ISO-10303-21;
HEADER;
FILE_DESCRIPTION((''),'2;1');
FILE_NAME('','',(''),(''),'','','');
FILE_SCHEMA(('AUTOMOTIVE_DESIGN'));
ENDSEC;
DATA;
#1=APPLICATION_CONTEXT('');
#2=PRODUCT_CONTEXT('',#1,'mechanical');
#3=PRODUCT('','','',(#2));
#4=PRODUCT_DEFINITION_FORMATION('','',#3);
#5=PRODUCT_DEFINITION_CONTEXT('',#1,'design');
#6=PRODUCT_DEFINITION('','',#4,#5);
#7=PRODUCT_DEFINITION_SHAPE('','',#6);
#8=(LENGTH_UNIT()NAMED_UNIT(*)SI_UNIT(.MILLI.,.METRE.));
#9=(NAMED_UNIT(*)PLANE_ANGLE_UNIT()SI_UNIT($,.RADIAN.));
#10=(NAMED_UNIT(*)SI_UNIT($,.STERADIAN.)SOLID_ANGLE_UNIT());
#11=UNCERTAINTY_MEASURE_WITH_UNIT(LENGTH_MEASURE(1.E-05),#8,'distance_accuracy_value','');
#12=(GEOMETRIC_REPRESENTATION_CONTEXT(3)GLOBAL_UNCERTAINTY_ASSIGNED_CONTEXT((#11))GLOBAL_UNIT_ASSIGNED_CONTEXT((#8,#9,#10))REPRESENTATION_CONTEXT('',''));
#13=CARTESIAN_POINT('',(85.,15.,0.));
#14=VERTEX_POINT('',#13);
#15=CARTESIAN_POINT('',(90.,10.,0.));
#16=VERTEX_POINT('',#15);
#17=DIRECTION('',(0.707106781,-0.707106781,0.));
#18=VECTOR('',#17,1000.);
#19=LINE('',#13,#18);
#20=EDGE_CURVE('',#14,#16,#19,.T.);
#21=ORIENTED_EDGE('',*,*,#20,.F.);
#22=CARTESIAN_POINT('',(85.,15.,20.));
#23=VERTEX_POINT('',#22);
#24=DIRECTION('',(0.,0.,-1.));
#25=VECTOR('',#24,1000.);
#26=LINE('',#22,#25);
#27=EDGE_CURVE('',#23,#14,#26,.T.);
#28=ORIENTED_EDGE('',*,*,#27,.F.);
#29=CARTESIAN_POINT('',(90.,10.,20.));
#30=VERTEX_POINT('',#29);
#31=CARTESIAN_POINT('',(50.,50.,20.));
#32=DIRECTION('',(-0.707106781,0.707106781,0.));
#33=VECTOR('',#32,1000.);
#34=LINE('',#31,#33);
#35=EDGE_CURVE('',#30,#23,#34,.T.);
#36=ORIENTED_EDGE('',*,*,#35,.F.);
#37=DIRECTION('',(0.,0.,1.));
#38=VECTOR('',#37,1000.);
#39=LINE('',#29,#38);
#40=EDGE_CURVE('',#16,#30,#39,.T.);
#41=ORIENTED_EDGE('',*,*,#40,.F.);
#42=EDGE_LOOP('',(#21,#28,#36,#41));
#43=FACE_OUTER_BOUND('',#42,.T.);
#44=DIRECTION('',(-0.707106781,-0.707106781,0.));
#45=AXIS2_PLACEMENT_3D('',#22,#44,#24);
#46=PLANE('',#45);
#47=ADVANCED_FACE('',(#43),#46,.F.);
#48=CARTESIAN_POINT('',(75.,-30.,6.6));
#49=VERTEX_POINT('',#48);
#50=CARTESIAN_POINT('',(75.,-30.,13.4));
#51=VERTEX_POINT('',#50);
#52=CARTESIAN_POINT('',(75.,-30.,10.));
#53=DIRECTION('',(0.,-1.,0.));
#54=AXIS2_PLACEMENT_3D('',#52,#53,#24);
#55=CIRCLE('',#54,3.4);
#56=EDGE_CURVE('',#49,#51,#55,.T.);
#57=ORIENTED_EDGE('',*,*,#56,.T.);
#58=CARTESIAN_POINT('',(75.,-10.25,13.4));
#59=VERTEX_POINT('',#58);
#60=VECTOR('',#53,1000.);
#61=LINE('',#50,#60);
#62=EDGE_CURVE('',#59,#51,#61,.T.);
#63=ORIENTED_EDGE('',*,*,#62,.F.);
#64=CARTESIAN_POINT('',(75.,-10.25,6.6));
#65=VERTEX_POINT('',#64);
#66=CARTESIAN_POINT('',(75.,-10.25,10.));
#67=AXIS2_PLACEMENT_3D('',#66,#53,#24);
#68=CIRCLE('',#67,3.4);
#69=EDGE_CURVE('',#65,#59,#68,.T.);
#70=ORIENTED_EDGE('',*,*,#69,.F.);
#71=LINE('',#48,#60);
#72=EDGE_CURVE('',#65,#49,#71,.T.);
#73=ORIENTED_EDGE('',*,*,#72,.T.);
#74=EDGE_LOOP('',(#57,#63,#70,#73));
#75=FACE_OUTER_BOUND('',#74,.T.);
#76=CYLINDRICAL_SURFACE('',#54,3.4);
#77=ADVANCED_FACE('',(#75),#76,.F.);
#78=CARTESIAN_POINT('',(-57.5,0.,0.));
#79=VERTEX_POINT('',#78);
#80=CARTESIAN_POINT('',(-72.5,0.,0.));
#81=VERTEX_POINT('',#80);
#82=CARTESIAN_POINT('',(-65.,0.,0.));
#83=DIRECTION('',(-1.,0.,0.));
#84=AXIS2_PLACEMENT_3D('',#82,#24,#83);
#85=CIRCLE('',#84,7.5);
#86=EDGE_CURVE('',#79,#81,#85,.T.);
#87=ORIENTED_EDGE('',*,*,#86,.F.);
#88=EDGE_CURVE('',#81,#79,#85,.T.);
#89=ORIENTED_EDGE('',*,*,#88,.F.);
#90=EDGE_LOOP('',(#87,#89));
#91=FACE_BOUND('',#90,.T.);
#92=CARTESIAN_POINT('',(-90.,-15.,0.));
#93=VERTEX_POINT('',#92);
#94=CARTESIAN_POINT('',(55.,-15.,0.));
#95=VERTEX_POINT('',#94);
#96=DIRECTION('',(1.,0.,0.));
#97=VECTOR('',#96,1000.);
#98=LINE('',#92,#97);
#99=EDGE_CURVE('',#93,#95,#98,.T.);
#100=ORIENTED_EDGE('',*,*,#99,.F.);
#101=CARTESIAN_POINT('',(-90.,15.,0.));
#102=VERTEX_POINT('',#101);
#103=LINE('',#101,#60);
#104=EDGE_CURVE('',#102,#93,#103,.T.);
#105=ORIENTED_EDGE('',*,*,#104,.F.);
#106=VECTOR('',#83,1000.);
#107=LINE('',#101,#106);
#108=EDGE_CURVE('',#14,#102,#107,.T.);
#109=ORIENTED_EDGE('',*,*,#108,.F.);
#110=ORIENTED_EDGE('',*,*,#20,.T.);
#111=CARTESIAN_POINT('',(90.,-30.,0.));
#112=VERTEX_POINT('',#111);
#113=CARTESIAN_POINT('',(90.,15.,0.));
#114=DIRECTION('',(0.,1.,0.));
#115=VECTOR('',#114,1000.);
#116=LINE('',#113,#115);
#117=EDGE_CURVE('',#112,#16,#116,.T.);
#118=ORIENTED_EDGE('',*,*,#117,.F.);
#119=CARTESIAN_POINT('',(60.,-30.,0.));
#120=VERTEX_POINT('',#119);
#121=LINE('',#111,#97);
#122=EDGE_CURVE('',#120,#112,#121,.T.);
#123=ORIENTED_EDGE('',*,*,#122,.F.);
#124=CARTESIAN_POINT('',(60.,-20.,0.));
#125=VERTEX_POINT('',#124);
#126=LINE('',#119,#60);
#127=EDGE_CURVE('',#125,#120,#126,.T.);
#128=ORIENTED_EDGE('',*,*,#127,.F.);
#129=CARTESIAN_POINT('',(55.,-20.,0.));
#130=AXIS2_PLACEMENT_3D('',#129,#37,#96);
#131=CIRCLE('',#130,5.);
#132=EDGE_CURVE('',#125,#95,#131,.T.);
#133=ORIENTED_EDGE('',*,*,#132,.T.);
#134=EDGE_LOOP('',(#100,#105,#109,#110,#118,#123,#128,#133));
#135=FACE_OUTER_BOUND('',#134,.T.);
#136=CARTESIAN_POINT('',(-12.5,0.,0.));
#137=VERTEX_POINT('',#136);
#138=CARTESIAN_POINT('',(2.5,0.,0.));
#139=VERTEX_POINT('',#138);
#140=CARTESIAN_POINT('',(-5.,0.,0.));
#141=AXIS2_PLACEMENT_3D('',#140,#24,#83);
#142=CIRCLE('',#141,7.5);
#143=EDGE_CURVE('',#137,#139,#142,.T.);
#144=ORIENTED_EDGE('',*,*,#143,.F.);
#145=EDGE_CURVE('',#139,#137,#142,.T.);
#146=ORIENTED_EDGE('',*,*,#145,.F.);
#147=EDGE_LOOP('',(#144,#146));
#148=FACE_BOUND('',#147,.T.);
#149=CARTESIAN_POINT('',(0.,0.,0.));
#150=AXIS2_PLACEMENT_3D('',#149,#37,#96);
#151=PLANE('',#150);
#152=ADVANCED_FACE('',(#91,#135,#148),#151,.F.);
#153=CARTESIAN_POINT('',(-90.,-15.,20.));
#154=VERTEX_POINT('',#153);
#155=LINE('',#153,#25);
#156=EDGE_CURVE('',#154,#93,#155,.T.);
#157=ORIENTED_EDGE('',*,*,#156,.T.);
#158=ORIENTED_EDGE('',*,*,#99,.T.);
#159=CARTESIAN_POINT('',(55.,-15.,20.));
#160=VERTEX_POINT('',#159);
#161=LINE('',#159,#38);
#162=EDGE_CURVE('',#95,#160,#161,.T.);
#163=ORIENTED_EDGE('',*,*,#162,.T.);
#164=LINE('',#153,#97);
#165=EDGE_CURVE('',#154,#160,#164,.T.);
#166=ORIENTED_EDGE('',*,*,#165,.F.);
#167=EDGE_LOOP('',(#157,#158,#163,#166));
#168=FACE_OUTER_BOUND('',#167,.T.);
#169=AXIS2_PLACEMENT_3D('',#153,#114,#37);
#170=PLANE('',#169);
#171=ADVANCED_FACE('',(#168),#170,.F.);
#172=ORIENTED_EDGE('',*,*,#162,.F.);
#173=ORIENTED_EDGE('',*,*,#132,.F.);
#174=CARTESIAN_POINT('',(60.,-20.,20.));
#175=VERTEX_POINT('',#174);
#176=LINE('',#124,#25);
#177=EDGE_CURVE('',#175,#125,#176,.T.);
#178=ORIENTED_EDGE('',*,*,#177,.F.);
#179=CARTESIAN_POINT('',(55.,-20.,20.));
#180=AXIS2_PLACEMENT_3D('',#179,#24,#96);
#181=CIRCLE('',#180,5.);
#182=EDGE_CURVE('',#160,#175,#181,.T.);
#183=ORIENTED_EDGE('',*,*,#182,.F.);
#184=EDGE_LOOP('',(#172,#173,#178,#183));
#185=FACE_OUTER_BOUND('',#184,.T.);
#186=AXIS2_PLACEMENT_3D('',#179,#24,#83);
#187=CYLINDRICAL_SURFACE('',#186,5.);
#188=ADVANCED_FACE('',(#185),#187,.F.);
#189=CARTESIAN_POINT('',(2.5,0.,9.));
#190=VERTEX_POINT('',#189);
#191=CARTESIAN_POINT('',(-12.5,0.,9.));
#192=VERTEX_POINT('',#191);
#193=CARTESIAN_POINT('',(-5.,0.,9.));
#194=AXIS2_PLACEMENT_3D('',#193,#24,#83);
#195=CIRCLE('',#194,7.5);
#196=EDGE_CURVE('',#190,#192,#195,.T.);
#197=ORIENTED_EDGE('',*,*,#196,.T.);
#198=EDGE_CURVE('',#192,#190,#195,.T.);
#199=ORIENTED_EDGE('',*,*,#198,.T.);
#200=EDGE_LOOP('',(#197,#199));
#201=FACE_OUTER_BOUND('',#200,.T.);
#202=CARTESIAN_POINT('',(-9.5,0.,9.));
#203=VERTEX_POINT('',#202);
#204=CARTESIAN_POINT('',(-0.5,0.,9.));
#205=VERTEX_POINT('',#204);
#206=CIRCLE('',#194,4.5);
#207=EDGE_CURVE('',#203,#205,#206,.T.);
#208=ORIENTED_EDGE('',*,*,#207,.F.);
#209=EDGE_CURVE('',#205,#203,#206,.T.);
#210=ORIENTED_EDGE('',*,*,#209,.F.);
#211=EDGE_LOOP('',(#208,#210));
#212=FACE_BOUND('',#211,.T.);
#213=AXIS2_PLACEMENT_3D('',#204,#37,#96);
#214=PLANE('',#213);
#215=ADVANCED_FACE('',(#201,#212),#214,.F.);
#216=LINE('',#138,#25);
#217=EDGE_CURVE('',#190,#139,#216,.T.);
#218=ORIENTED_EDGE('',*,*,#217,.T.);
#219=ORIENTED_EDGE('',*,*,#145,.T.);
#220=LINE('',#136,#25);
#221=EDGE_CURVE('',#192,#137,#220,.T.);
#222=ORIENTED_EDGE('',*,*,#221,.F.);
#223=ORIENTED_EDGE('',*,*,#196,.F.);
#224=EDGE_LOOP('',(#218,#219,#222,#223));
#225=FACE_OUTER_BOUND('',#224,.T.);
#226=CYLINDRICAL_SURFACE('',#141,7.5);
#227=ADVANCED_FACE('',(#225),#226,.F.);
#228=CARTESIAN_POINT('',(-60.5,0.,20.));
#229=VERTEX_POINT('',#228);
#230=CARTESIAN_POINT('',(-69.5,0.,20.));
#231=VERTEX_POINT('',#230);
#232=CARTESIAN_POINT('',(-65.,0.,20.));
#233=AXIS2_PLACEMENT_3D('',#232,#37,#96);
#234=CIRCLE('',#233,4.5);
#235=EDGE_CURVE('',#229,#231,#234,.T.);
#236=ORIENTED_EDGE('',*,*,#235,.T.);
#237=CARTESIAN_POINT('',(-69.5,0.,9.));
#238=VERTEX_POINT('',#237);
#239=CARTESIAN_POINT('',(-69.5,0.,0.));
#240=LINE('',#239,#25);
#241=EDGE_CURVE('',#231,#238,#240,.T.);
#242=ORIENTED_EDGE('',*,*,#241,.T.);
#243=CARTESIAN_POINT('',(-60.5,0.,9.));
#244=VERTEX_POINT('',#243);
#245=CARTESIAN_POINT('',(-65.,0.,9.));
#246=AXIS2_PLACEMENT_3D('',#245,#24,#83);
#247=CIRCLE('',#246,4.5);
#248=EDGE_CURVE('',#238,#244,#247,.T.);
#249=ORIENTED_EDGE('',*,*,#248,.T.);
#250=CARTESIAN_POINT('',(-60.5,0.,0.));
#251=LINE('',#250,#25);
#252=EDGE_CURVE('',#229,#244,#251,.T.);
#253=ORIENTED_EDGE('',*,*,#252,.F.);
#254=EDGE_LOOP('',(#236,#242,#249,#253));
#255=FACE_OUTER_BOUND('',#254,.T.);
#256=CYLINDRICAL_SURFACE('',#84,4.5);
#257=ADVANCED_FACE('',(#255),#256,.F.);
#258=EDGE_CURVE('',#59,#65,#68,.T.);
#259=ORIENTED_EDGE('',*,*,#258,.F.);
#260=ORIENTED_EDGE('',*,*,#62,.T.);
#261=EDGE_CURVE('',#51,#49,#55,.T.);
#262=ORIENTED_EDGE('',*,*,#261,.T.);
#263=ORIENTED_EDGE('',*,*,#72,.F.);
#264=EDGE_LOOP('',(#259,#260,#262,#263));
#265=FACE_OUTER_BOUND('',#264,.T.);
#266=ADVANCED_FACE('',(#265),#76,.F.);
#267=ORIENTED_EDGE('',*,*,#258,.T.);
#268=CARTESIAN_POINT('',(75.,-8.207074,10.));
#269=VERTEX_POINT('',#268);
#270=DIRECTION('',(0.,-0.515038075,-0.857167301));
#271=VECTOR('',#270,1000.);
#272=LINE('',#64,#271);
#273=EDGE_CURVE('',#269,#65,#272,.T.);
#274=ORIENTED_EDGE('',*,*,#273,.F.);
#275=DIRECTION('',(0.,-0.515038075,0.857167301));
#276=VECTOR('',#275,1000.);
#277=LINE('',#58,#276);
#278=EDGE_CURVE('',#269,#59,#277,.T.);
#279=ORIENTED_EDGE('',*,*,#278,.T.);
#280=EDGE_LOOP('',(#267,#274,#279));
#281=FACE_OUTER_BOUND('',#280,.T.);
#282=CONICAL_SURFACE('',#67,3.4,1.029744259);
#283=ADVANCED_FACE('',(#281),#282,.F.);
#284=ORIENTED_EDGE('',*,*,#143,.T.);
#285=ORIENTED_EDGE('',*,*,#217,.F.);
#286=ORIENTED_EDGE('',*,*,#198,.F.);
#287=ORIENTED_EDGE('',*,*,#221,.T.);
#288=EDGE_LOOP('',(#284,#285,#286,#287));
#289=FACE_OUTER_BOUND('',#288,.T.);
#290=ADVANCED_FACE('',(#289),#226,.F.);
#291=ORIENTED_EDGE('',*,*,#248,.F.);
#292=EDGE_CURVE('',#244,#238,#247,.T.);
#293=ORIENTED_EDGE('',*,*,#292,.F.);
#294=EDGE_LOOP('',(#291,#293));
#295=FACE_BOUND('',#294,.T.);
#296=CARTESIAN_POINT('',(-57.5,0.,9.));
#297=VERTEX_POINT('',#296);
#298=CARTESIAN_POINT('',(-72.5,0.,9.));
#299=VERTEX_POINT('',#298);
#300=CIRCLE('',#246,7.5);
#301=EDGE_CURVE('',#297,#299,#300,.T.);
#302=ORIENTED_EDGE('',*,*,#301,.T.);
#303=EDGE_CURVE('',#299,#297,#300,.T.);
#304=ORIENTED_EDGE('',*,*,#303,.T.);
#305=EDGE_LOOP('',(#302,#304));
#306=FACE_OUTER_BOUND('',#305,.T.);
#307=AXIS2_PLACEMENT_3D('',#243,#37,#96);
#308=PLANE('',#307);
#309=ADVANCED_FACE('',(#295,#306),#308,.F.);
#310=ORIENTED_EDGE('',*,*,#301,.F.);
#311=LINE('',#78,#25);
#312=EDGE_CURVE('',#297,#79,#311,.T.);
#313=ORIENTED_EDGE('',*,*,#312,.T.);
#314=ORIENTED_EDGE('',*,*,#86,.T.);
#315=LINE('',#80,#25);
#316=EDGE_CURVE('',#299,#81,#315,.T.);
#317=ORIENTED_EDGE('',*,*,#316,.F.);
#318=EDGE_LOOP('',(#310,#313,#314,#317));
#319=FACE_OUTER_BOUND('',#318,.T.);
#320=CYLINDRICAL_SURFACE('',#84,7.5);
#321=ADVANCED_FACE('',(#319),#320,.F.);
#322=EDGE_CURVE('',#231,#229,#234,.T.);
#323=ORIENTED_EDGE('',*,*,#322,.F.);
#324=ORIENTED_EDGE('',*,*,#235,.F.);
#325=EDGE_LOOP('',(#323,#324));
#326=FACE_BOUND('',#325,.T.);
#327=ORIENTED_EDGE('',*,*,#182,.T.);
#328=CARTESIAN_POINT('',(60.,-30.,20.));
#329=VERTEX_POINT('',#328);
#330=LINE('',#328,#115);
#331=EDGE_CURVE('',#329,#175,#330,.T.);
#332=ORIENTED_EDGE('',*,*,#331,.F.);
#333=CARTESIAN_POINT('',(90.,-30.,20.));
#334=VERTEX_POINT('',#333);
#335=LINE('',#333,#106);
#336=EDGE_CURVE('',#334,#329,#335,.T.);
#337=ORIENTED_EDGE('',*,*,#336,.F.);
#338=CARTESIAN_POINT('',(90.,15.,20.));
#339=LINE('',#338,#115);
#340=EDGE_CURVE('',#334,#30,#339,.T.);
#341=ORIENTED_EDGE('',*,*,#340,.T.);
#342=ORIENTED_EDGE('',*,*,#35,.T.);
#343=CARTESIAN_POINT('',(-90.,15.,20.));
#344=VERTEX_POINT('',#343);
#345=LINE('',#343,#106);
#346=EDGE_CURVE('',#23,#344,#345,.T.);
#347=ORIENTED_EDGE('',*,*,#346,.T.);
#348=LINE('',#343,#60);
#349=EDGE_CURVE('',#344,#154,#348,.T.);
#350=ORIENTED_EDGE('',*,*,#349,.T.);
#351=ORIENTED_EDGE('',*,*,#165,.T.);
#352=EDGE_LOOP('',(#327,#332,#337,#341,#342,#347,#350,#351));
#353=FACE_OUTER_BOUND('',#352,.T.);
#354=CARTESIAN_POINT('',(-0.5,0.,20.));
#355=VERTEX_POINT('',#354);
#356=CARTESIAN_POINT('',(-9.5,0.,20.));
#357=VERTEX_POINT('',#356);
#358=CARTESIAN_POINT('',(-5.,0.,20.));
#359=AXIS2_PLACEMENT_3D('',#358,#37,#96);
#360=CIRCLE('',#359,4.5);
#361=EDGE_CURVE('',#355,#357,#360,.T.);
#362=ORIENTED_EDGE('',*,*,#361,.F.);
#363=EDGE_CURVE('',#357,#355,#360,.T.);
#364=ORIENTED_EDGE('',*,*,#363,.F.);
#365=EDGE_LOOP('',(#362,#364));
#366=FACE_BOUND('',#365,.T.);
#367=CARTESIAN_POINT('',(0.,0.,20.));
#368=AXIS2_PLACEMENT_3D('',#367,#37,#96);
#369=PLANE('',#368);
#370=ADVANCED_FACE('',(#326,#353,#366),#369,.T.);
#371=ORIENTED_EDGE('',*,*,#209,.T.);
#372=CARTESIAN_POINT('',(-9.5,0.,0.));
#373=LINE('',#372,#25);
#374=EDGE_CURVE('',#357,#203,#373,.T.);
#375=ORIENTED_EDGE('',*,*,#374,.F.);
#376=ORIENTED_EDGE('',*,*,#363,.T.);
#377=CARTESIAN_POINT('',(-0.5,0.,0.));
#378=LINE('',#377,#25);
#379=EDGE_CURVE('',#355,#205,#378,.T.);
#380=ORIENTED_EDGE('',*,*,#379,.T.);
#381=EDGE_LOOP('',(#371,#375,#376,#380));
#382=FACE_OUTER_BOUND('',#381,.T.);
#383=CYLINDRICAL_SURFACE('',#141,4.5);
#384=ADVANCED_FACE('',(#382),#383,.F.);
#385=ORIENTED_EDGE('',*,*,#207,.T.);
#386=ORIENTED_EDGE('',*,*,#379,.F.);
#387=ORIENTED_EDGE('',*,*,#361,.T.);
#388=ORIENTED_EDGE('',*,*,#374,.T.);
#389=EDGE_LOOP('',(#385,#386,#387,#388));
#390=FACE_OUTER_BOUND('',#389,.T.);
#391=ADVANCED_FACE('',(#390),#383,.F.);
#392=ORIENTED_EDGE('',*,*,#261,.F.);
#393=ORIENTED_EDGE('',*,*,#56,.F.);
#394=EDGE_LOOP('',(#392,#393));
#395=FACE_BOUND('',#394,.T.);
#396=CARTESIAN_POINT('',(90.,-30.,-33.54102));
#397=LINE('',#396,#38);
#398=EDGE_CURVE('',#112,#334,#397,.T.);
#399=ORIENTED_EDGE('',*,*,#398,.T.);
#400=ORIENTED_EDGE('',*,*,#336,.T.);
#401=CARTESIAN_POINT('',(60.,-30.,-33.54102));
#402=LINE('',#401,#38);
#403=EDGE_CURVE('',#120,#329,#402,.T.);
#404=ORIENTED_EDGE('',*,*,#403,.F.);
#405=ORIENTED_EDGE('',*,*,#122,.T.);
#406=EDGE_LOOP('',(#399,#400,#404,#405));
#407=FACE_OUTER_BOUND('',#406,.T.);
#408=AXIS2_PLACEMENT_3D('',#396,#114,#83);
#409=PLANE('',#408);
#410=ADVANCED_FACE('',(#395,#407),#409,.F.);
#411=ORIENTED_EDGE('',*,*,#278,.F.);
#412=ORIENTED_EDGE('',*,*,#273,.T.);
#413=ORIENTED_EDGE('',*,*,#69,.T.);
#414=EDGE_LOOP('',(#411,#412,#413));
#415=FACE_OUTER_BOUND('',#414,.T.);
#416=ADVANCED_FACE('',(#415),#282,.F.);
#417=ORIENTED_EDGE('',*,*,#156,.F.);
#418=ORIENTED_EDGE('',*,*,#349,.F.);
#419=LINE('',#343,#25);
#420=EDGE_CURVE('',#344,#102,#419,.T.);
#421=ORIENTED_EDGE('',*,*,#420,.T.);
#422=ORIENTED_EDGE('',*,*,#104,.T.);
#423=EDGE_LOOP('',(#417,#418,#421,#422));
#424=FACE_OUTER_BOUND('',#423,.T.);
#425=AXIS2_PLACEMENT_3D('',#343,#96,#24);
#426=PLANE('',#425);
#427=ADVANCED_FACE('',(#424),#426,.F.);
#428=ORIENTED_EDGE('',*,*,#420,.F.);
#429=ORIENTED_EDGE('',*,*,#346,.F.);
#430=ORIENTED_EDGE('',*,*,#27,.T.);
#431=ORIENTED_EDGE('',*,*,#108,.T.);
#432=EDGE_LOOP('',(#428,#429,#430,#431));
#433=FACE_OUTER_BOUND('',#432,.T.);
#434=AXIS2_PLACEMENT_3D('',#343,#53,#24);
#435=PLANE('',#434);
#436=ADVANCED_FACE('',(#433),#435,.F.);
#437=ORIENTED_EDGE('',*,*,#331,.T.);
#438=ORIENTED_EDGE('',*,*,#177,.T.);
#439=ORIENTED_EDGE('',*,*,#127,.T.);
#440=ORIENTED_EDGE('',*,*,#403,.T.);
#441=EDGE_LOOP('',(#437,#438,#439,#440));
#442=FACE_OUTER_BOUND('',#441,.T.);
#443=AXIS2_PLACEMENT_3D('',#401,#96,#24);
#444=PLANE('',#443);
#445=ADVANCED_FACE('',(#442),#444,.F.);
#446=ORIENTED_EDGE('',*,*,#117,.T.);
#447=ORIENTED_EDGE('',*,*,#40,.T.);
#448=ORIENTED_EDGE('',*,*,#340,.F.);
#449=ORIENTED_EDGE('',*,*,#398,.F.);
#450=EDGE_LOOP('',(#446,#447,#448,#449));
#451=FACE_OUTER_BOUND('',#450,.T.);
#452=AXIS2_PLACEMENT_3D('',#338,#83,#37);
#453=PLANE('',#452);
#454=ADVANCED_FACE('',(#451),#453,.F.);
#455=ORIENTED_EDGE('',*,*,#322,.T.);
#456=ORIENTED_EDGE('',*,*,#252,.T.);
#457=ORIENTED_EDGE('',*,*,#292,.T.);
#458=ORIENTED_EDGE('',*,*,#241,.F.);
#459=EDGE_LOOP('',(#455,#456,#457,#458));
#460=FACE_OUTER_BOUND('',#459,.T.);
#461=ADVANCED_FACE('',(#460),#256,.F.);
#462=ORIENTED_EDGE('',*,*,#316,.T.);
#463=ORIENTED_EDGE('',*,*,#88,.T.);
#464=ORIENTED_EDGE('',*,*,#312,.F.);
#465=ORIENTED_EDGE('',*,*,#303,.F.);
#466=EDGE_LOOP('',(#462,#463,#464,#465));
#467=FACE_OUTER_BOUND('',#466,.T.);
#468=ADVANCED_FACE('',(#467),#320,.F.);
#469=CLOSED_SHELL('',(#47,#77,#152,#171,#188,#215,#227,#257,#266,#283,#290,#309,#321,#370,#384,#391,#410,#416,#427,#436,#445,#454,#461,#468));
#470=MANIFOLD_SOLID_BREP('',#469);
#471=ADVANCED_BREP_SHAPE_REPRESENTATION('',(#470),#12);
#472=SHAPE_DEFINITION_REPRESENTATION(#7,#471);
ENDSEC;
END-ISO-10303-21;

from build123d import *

# Parameters (mm, degrees)
SKETCH_1_W                = 180
SKETCH_1_H                = 30
EXTRUDE_1_DEPTH           = 20
SKETCH_4_W                = 30
SKETCH_4_H                = 15
EXTRUDE_2_DEPTH           = 20
FILLET_1_R                = 5
CHAMFER_1_SIZE            = 5
HOLE_WIZARD_M8_2_D        = 6.8
HOLE_WIZARD_M8_2_DEPTH    = 19.75
HOLE_WIZARD_M8_2_TIP      = 2.042926105
HOLE_WIZARD_1_D           = 9
HOLE_WIZARD_1_DEPTH       = 27.5
HOLE_WIZARD_1_CBORE_D     = 15
HOLE_WIZARD_1_CBORE_DEPTH = 9
HOLE_WIZARD_1_TIP         = 2.703872786


with BuildPart() as part:
    # 草图1 → 凸台-拉伸1 (new body)
    with BuildSketch(Plane.XY):
        Rectangle(SKETCH_1_W, SKETCH_1_H)
    extrude(amount=EXTRUDE_1_DEPTH)

    # 草图4 → 凸台-拉伸2 (add)
    with BuildSketch(Plane.XY.offset(20)):
        with Locations((75, -22.5)):
            Rectangle(SKETCH_4_W, SKETCH_4_H)
    extrude(amount=-EXTRUDE_2_DEPTH)

    # 圆角1
    fillet_1_edges = [part.edges().sort_by_distance(p)[0] for p in [
        (60, -15, 10),
    ]]
    fillet(fillet_1_edges, radius=FILLET_1_R)

    # 倒角1
    chamfer_1_edges = [part.edges().sort_by_distance(p)[0] for p in [
        (90, 15, 10),
    ]]
    chamfer(chamfer_1_edges, length=CHAMFER_1_SIZE)

    # M8 螺纹孔2
    with Locations(Plane(origin=(0, -30, 0), x_dir=(-1, 0, 0), z_dir=(0, -1, 0))):
        with Locations((-75, -10)):
            Hole(HOLE_WIZARD_M8_2_D / 2, depth=HOLE_WIZARD_M8_2_DEPTH)
            with Locations((0, 0, -(HOLE_WIZARD_M8_2_DEPTH + HOLE_WIZARD_M8_2_TIP / 2))):  # 118° drill point
                Cone(0, HOLE_WIZARD_M8_2_D / 2, HOLE_WIZARD_M8_2_TIP, mode=Mode.SUBTRACT)

    # 打孔尺寸(%根据)内六角圆柱头螺钉的类型1
    with Locations(Plane(origin=(0, 0, 0), x_dir=(-1, 0, 0), z_dir=(0, 0, -1))):
        with Locations((65, 0), (5, 0)):
            CounterBoreHole(HOLE_WIZARD_1_D / 2, HOLE_WIZARD_1_CBORE_D / 2, HOLE_WIZARD_1_CBORE_DEPTH, depth=HOLE_WIZARD_1_DEPTH)
            with Locations((0, 0, -(HOLE_WIZARD_1_DEPTH + HOLE_WIZARD_1_TIP / 2))):  # 118° drill point
                Cone(0, HOLE_WIZARD_1_D / 2, HOLE_WIZARD_1_TIP, mode=Mode.SUBTRACT)


solid = part.part
